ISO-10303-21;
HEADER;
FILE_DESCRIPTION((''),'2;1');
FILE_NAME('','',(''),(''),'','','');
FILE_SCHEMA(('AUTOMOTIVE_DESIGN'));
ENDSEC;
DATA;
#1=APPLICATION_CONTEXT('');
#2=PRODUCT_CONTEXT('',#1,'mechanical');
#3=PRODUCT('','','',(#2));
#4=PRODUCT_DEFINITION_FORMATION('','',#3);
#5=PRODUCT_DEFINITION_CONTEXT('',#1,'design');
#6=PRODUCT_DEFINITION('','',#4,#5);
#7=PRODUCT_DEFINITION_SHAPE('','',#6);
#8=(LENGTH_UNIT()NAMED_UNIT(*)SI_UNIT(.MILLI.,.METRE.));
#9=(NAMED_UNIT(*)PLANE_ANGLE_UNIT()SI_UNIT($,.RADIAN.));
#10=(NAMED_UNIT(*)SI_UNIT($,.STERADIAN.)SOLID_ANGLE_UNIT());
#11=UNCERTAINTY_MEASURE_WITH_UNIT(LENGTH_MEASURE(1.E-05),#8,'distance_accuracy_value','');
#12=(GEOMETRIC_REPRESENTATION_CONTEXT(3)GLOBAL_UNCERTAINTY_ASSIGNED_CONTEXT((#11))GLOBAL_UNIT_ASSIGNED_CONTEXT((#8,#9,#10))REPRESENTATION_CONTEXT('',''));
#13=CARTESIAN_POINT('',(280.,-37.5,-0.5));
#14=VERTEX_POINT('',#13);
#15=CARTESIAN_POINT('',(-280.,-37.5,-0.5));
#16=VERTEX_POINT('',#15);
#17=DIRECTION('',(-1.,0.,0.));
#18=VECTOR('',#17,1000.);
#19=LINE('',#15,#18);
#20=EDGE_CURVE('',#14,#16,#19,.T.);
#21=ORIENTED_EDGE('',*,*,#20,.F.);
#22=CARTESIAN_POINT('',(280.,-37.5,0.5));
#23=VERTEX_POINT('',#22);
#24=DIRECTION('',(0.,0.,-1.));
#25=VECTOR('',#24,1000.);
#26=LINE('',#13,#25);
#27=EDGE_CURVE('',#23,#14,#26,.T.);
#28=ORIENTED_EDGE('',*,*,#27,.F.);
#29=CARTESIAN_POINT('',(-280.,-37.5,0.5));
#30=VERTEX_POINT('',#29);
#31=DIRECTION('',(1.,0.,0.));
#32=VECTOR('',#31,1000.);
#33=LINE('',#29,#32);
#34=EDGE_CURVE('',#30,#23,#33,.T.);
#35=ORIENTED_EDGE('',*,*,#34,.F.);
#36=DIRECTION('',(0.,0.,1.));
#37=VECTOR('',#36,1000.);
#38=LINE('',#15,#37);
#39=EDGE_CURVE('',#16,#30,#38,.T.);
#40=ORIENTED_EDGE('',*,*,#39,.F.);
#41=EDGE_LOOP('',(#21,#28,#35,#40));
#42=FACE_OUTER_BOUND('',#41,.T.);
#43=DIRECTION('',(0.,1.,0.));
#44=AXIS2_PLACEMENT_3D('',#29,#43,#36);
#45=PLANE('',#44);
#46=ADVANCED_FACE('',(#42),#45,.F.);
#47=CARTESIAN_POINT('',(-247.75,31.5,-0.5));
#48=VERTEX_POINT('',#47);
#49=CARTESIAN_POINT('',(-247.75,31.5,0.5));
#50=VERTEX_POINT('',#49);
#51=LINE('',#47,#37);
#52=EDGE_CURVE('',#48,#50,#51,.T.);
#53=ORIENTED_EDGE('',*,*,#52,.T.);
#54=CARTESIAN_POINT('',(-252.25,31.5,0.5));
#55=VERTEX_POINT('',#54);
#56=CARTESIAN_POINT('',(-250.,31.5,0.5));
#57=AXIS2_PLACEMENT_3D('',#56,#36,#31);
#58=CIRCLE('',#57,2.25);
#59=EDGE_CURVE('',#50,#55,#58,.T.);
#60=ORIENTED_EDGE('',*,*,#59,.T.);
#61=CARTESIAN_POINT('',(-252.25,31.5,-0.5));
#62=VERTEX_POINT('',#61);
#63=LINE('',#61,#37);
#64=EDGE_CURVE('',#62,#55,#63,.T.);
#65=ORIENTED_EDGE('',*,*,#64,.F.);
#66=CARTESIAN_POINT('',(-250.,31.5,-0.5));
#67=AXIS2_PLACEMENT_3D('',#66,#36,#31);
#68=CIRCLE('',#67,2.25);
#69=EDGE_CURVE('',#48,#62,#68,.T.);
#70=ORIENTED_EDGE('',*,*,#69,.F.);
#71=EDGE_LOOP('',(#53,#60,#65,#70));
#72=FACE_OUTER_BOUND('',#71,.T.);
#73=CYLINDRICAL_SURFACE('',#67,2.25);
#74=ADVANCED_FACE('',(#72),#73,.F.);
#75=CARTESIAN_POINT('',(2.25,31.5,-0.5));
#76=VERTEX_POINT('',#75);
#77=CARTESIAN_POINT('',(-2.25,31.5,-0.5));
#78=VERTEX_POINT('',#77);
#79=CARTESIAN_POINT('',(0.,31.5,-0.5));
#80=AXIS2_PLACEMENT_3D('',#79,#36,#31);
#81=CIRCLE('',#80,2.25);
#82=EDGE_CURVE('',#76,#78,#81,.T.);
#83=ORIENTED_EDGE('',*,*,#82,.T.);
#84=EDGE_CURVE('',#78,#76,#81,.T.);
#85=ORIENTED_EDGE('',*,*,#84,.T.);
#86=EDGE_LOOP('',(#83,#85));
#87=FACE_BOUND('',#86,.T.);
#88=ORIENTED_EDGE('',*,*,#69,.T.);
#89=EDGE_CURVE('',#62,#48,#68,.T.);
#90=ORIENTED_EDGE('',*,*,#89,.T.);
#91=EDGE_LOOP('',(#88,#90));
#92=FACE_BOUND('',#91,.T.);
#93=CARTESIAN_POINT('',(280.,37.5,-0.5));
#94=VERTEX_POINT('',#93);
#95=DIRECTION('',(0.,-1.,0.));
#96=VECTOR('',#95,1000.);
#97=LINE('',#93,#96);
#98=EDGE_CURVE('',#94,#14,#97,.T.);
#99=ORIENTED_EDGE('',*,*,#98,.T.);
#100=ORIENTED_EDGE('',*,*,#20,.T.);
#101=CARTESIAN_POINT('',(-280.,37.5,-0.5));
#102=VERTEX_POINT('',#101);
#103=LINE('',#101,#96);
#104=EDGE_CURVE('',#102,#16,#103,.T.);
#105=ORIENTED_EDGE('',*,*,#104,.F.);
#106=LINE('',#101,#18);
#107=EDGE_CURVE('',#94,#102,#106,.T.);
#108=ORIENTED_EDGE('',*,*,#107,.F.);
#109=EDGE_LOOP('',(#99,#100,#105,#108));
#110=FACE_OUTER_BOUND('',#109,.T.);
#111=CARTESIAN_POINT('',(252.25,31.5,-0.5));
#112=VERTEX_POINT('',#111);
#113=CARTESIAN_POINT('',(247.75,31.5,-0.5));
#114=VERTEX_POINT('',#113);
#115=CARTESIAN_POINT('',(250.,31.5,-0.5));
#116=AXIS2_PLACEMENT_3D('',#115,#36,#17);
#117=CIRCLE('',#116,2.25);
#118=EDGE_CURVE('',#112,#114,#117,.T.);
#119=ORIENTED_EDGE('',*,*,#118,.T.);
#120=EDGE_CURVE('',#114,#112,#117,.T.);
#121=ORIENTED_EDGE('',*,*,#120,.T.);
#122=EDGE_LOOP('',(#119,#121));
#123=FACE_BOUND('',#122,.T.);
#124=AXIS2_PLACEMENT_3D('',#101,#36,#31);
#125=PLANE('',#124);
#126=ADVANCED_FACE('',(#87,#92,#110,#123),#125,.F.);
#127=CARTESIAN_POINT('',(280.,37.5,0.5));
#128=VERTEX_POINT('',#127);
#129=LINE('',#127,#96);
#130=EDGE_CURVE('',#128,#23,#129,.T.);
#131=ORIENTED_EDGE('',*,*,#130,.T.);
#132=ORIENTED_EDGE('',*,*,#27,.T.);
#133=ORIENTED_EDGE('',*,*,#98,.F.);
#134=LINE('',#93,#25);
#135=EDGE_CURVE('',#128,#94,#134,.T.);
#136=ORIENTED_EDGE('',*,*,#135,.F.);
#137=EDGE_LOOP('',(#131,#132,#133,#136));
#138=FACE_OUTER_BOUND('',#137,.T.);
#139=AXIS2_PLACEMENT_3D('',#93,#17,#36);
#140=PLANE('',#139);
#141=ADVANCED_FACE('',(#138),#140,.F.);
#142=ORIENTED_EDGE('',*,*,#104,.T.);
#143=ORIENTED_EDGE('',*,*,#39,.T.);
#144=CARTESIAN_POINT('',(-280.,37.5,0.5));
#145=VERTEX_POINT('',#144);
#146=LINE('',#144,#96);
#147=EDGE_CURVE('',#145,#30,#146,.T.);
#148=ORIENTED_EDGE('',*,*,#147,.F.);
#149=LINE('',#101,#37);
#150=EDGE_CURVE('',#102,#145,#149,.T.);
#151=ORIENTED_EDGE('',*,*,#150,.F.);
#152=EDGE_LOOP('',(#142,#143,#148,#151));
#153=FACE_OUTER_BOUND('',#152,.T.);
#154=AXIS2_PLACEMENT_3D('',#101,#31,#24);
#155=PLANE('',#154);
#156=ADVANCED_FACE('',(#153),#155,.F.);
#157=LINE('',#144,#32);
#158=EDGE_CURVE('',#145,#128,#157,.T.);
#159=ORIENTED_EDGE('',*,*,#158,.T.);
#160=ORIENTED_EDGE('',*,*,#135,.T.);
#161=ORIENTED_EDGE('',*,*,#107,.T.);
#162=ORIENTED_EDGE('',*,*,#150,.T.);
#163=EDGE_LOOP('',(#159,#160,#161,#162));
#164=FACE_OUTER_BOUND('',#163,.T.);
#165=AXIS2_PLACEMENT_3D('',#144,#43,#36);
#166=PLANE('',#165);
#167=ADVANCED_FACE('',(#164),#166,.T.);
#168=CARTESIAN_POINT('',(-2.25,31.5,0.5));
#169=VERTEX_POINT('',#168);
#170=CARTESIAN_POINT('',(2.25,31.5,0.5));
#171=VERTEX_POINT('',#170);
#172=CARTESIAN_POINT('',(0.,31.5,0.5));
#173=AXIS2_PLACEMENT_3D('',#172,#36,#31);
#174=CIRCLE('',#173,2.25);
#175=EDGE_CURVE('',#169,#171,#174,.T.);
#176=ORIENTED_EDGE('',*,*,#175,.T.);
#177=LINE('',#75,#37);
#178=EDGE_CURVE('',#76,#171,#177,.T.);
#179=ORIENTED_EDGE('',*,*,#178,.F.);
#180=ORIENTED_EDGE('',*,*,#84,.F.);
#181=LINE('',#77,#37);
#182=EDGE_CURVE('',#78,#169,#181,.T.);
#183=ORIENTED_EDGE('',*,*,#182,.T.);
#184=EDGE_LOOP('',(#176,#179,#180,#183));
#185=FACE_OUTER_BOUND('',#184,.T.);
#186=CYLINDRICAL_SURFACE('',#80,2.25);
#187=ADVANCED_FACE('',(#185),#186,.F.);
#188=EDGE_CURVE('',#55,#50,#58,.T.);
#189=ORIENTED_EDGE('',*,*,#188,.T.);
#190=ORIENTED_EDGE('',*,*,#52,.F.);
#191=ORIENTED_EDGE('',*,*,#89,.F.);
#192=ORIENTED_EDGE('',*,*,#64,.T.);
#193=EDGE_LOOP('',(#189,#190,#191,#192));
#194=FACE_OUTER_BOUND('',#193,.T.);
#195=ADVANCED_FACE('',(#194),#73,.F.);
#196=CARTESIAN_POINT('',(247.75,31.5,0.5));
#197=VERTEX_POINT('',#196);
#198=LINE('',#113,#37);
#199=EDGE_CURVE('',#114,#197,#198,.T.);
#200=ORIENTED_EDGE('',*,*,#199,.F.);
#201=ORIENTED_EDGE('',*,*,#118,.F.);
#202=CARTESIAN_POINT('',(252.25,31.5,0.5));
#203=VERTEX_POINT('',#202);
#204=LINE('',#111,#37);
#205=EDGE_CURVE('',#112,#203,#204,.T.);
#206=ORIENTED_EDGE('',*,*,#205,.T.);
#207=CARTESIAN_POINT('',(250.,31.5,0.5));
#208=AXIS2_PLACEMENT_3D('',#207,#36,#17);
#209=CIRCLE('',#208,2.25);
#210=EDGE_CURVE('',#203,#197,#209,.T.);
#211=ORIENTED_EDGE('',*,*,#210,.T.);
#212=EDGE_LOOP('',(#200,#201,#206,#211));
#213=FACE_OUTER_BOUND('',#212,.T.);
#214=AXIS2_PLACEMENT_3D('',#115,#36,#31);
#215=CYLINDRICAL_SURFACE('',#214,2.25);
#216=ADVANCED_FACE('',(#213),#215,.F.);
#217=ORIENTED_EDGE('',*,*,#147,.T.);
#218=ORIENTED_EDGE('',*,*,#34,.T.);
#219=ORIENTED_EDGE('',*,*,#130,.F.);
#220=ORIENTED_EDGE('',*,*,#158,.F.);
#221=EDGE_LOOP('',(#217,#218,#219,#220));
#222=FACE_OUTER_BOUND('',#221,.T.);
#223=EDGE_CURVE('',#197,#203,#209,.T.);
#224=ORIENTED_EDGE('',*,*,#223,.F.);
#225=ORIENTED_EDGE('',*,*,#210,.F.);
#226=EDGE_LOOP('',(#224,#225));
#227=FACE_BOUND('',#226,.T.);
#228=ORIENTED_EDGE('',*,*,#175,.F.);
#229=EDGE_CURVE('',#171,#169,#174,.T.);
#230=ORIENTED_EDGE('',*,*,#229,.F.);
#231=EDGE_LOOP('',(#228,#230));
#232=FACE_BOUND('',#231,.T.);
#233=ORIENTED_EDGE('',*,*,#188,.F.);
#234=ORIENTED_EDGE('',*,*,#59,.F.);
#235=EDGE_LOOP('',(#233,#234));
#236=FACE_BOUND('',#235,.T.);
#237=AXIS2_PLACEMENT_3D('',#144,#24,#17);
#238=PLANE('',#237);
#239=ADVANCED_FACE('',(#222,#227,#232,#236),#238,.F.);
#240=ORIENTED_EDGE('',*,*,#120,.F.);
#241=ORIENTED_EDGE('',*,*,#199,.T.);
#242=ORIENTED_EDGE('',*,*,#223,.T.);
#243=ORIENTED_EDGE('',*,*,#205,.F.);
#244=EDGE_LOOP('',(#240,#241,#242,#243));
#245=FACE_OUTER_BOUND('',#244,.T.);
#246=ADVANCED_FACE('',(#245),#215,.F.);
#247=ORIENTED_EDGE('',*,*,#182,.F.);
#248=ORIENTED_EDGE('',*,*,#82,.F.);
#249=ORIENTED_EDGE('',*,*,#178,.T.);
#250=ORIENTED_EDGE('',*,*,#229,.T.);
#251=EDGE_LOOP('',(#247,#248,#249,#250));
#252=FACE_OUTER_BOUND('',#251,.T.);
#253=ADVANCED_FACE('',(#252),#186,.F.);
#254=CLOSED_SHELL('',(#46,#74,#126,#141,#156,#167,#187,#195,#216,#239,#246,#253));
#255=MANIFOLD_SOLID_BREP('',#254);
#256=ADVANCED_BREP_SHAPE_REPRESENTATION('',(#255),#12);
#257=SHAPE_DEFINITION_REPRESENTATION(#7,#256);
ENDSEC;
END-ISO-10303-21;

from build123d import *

# Parameters (mm, degrees)
SKETCH1_W          = 560
SKETCH1_H          = 1
EXTRUDE1_DEPTH     = 37.5
SKETCH3_R          = 2.25
CUT_EXTRUDE1_DEPTH = 283.501769906


with BuildPart() as part:
    # Sketch1 → Extrude1 (new, symmetric)
    with BuildSketch(Plane(origin=(0, 0, 0), x_dir=(1, 0, 0), z_dir=(0, 1, 0))):
        Rectangle(SKETCH1_W, SKETCH1_H)
    extrude(amount=EXTRUDE1_DEPTH, both=True)

    # Sketch3 → Cut-Extrude1 (cut, through all)
    with BuildSketch(Plane.XY.offset(0.5)):
        with Locations((-250, 31.5)):
            Circle(SKETCH3_R)
        with Locations(Location((250, 31.5, 0), (0, 0, 180))):
            Circle(SKETCH3_R)
        with Locations((0, 31.5)):
            Circle(SKETCH3_R)
    extrude(amount=-CUT_EXTRUDE1_DEPTH, mode=Mode.SUBTRACT)


solid = part.part
